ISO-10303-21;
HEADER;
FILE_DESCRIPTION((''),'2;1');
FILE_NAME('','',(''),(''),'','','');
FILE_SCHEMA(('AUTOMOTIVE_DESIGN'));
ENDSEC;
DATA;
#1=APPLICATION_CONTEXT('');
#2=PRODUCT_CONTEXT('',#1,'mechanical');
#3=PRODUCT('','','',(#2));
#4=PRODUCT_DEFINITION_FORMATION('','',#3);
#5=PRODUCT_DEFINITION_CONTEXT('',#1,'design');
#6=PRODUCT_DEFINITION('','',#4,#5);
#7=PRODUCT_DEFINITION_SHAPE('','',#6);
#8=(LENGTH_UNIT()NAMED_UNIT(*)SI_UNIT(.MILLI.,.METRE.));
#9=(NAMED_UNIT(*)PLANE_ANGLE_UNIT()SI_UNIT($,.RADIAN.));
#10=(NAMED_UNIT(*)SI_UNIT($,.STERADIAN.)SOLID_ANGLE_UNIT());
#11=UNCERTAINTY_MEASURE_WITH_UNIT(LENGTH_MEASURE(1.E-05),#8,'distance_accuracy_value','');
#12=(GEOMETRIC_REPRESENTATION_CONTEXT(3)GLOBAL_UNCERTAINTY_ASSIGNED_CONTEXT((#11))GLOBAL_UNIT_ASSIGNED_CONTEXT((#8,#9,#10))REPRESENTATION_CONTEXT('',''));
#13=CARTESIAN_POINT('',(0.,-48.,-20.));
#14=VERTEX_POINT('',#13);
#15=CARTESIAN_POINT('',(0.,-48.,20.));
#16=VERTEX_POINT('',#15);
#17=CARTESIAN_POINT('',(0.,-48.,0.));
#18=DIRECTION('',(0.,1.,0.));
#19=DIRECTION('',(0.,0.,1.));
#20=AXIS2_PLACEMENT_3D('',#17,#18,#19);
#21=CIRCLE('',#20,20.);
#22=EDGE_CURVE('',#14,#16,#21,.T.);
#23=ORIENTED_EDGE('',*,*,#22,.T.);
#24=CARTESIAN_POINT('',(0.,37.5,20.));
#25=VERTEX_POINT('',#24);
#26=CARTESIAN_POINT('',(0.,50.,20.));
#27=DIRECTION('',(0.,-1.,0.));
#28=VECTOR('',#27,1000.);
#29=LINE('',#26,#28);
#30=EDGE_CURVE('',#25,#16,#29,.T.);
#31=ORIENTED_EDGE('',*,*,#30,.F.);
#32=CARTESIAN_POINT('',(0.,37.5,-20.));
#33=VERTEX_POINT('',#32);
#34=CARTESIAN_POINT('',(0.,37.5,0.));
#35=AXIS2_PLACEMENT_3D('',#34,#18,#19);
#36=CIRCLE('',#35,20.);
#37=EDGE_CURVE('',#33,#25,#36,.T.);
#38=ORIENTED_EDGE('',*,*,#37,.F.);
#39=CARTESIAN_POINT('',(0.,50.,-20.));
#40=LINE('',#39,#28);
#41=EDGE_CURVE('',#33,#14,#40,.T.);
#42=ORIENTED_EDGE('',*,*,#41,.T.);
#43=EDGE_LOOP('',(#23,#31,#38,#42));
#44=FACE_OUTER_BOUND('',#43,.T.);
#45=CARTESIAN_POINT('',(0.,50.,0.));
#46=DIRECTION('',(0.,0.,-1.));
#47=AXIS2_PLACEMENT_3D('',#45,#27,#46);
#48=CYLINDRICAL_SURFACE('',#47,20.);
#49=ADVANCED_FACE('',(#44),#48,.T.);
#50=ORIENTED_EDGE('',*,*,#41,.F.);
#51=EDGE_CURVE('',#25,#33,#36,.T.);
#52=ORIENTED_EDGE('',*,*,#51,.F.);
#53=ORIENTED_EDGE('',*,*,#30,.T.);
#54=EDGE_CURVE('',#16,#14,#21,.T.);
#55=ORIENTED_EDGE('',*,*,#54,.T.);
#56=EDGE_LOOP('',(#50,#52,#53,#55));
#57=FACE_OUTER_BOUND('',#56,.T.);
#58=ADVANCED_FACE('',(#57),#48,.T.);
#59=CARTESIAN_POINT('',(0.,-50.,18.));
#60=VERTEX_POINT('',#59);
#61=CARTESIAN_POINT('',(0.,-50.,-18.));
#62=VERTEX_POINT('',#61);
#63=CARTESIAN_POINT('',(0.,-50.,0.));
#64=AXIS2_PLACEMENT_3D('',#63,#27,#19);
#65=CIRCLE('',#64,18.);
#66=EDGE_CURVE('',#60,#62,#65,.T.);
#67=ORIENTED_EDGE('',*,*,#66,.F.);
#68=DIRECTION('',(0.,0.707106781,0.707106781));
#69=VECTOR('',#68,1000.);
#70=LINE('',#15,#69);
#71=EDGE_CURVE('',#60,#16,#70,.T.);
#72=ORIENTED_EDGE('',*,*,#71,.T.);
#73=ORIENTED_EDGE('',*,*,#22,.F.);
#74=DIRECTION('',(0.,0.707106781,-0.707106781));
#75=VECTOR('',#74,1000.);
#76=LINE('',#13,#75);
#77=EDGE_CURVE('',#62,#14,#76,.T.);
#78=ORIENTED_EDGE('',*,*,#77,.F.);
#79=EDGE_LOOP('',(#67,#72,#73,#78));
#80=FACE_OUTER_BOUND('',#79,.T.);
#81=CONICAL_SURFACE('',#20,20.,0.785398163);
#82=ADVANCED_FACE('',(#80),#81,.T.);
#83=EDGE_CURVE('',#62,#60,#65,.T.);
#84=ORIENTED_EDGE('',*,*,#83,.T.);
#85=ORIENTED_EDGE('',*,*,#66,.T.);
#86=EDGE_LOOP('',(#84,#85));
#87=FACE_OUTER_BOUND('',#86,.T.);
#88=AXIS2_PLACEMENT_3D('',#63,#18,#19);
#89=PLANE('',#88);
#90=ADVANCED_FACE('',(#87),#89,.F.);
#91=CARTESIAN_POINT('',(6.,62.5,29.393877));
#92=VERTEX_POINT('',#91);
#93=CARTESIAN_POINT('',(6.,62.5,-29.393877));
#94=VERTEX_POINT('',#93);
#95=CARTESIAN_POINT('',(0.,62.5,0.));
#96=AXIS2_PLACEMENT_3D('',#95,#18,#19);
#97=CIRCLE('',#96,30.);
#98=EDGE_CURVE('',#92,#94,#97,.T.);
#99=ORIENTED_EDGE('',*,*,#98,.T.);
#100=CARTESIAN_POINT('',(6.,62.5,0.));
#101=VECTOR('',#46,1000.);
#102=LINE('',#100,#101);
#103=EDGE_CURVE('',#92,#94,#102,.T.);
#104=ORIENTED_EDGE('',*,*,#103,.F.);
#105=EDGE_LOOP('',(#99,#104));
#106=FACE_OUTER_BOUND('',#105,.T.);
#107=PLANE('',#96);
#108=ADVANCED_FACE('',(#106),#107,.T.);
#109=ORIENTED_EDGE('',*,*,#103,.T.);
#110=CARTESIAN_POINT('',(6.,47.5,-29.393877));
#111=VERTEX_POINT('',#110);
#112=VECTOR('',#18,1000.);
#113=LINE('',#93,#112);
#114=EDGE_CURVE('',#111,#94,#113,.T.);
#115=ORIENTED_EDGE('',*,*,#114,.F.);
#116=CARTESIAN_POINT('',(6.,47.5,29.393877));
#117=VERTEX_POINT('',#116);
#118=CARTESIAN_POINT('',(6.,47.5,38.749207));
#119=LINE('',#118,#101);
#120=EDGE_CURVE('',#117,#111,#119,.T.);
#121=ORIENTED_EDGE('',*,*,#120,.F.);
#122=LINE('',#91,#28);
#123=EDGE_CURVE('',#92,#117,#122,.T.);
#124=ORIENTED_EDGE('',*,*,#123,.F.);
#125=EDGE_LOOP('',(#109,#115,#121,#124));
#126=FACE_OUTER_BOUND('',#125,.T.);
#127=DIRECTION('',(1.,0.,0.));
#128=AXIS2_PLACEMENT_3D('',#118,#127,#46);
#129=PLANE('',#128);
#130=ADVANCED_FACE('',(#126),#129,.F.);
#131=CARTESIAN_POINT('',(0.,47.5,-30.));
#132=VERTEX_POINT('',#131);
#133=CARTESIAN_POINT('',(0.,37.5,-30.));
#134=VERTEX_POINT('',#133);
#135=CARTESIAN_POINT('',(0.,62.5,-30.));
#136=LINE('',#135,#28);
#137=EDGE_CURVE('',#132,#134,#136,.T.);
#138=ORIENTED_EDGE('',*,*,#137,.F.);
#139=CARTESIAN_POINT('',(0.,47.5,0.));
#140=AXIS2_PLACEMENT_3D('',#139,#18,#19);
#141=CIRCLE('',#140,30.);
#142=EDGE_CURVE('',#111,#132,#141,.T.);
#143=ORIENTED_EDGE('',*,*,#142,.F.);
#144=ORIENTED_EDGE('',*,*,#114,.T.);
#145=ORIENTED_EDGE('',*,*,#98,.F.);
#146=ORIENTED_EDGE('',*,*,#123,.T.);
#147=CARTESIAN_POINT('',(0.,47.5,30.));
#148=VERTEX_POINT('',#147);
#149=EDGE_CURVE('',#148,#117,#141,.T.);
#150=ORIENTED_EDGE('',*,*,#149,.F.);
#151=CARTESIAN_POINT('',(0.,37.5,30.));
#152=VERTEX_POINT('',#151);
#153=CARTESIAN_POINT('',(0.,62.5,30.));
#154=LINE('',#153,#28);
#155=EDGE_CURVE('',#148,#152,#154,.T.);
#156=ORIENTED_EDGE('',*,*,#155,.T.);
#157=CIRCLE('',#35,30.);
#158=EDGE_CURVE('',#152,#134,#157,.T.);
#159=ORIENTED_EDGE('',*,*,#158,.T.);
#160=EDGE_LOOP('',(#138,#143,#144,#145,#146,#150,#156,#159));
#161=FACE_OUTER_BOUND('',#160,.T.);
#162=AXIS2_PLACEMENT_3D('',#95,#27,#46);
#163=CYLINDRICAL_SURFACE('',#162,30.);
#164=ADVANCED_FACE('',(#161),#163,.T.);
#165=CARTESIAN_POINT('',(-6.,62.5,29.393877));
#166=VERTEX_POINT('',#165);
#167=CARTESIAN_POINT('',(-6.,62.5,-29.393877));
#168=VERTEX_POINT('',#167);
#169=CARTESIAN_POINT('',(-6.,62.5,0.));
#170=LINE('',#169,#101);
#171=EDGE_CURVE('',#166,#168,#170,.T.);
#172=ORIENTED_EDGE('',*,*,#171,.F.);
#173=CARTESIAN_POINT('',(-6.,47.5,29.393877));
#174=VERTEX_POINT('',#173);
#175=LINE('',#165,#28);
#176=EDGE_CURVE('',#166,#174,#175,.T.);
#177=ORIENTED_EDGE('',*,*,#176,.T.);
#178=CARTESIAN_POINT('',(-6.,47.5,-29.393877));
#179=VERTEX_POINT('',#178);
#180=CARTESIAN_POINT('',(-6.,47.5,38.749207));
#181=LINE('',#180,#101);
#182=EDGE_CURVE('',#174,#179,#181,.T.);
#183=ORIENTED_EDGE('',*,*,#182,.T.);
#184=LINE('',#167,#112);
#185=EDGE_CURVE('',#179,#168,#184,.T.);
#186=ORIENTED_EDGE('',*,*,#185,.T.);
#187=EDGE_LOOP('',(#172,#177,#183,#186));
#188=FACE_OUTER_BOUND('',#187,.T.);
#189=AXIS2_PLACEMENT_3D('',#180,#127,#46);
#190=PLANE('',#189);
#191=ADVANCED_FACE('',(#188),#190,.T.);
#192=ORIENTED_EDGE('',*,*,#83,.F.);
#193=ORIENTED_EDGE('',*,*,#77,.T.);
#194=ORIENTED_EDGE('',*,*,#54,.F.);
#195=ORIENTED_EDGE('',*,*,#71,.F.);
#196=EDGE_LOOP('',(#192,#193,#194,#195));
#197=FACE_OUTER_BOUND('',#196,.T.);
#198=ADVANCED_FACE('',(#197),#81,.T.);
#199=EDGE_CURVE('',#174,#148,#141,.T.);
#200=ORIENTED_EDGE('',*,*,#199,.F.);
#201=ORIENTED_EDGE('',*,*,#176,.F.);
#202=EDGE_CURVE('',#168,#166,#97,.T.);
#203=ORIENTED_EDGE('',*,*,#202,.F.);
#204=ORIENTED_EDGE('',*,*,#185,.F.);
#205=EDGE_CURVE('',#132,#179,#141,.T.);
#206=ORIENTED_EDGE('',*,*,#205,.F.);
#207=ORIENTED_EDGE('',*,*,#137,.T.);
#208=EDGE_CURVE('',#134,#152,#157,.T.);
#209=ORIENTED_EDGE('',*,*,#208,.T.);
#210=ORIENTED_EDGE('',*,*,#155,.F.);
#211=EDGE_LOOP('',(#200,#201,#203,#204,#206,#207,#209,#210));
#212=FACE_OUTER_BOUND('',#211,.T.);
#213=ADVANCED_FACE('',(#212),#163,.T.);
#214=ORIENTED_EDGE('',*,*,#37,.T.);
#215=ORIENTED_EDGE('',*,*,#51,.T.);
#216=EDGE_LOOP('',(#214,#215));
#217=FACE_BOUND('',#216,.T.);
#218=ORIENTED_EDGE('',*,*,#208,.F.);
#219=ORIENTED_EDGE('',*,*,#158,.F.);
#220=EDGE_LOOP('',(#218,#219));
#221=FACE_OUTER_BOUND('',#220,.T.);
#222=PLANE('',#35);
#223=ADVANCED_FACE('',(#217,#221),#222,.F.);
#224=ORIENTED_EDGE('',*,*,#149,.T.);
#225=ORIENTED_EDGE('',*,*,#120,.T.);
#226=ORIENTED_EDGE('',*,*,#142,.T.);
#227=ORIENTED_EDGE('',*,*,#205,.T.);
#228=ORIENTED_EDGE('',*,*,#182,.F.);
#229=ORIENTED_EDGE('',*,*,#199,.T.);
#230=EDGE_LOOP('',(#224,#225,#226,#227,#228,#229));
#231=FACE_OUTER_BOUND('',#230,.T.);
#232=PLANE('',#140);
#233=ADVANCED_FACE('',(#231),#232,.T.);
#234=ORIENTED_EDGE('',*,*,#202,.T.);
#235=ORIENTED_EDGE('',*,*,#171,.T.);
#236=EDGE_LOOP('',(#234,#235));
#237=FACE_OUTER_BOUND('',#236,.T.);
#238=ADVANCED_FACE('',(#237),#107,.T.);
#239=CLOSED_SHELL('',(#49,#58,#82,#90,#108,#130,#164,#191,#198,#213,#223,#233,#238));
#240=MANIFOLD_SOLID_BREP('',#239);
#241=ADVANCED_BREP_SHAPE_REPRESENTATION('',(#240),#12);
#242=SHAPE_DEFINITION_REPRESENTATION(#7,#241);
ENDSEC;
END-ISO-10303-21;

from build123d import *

# Parameters (mm, degrees)
SKETCH_1_R          = 20
EXTRUDE_1_DEPTH     = 50
SKETCH_2_R          = 30
EXTRUDE_2_DEPTH     = 12.5
CHAMFER_1_SIZE      = 2
SKETCH_3_W          = 12
SKETCH_3_H          = 77.498414616
CUT_EXTRUDE_1_DEPTH = 15


with BuildPart() as part:
    # 草图1 → 凸台-拉伸1 (new, symmetric)
    with BuildSketch(Plane(origin=(0, 0, 0), x_dir=(1, 0, 0), z_dir=(0, 1, 0))):
        with Locations(Location((0, 0, 0), (0, 0, 270))):
            Circle(SKETCH_1_R)
    extrude(amount=EXTRUDE_1_DEPTH, both=True)

    # 草图2 → 凸台-拉伸2 (add, symmetric)
    with BuildSketch(Plane(origin=(0, 50, 0), x_dir=(1, 0, 0), z_dir=(0, 1, 0))):
        with Locations(Location((0, 0, 0), (0, 0, 270))):
            Circle(SKETCH_2_R)
    extrude(amount=EXTRUDE_2_DEPTH, both=True)

    # 倒角1
    chamfer_1_edges = [part.edges().sort_by_distance(p)[0] for p in [
        (0, -50, -20),
    ]]
    chamfer(chamfer_1_edges, length=CHAMFER_1_SIZE)

    # 草图3 → 切除-拉伸1 (cut)
    with BuildSketch(Plane(origin=(0, 62.5, 0), x_dir=(1, 0, 0), z_dir=(0, 1, 0))):
        Rectangle(SKETCH_3_W, SKETCH_3_H)
    extrude(amount=-CUT_EXTRUDE_1_DEPTH, mode=Mode.SUBTRACT)


solid = part.part
